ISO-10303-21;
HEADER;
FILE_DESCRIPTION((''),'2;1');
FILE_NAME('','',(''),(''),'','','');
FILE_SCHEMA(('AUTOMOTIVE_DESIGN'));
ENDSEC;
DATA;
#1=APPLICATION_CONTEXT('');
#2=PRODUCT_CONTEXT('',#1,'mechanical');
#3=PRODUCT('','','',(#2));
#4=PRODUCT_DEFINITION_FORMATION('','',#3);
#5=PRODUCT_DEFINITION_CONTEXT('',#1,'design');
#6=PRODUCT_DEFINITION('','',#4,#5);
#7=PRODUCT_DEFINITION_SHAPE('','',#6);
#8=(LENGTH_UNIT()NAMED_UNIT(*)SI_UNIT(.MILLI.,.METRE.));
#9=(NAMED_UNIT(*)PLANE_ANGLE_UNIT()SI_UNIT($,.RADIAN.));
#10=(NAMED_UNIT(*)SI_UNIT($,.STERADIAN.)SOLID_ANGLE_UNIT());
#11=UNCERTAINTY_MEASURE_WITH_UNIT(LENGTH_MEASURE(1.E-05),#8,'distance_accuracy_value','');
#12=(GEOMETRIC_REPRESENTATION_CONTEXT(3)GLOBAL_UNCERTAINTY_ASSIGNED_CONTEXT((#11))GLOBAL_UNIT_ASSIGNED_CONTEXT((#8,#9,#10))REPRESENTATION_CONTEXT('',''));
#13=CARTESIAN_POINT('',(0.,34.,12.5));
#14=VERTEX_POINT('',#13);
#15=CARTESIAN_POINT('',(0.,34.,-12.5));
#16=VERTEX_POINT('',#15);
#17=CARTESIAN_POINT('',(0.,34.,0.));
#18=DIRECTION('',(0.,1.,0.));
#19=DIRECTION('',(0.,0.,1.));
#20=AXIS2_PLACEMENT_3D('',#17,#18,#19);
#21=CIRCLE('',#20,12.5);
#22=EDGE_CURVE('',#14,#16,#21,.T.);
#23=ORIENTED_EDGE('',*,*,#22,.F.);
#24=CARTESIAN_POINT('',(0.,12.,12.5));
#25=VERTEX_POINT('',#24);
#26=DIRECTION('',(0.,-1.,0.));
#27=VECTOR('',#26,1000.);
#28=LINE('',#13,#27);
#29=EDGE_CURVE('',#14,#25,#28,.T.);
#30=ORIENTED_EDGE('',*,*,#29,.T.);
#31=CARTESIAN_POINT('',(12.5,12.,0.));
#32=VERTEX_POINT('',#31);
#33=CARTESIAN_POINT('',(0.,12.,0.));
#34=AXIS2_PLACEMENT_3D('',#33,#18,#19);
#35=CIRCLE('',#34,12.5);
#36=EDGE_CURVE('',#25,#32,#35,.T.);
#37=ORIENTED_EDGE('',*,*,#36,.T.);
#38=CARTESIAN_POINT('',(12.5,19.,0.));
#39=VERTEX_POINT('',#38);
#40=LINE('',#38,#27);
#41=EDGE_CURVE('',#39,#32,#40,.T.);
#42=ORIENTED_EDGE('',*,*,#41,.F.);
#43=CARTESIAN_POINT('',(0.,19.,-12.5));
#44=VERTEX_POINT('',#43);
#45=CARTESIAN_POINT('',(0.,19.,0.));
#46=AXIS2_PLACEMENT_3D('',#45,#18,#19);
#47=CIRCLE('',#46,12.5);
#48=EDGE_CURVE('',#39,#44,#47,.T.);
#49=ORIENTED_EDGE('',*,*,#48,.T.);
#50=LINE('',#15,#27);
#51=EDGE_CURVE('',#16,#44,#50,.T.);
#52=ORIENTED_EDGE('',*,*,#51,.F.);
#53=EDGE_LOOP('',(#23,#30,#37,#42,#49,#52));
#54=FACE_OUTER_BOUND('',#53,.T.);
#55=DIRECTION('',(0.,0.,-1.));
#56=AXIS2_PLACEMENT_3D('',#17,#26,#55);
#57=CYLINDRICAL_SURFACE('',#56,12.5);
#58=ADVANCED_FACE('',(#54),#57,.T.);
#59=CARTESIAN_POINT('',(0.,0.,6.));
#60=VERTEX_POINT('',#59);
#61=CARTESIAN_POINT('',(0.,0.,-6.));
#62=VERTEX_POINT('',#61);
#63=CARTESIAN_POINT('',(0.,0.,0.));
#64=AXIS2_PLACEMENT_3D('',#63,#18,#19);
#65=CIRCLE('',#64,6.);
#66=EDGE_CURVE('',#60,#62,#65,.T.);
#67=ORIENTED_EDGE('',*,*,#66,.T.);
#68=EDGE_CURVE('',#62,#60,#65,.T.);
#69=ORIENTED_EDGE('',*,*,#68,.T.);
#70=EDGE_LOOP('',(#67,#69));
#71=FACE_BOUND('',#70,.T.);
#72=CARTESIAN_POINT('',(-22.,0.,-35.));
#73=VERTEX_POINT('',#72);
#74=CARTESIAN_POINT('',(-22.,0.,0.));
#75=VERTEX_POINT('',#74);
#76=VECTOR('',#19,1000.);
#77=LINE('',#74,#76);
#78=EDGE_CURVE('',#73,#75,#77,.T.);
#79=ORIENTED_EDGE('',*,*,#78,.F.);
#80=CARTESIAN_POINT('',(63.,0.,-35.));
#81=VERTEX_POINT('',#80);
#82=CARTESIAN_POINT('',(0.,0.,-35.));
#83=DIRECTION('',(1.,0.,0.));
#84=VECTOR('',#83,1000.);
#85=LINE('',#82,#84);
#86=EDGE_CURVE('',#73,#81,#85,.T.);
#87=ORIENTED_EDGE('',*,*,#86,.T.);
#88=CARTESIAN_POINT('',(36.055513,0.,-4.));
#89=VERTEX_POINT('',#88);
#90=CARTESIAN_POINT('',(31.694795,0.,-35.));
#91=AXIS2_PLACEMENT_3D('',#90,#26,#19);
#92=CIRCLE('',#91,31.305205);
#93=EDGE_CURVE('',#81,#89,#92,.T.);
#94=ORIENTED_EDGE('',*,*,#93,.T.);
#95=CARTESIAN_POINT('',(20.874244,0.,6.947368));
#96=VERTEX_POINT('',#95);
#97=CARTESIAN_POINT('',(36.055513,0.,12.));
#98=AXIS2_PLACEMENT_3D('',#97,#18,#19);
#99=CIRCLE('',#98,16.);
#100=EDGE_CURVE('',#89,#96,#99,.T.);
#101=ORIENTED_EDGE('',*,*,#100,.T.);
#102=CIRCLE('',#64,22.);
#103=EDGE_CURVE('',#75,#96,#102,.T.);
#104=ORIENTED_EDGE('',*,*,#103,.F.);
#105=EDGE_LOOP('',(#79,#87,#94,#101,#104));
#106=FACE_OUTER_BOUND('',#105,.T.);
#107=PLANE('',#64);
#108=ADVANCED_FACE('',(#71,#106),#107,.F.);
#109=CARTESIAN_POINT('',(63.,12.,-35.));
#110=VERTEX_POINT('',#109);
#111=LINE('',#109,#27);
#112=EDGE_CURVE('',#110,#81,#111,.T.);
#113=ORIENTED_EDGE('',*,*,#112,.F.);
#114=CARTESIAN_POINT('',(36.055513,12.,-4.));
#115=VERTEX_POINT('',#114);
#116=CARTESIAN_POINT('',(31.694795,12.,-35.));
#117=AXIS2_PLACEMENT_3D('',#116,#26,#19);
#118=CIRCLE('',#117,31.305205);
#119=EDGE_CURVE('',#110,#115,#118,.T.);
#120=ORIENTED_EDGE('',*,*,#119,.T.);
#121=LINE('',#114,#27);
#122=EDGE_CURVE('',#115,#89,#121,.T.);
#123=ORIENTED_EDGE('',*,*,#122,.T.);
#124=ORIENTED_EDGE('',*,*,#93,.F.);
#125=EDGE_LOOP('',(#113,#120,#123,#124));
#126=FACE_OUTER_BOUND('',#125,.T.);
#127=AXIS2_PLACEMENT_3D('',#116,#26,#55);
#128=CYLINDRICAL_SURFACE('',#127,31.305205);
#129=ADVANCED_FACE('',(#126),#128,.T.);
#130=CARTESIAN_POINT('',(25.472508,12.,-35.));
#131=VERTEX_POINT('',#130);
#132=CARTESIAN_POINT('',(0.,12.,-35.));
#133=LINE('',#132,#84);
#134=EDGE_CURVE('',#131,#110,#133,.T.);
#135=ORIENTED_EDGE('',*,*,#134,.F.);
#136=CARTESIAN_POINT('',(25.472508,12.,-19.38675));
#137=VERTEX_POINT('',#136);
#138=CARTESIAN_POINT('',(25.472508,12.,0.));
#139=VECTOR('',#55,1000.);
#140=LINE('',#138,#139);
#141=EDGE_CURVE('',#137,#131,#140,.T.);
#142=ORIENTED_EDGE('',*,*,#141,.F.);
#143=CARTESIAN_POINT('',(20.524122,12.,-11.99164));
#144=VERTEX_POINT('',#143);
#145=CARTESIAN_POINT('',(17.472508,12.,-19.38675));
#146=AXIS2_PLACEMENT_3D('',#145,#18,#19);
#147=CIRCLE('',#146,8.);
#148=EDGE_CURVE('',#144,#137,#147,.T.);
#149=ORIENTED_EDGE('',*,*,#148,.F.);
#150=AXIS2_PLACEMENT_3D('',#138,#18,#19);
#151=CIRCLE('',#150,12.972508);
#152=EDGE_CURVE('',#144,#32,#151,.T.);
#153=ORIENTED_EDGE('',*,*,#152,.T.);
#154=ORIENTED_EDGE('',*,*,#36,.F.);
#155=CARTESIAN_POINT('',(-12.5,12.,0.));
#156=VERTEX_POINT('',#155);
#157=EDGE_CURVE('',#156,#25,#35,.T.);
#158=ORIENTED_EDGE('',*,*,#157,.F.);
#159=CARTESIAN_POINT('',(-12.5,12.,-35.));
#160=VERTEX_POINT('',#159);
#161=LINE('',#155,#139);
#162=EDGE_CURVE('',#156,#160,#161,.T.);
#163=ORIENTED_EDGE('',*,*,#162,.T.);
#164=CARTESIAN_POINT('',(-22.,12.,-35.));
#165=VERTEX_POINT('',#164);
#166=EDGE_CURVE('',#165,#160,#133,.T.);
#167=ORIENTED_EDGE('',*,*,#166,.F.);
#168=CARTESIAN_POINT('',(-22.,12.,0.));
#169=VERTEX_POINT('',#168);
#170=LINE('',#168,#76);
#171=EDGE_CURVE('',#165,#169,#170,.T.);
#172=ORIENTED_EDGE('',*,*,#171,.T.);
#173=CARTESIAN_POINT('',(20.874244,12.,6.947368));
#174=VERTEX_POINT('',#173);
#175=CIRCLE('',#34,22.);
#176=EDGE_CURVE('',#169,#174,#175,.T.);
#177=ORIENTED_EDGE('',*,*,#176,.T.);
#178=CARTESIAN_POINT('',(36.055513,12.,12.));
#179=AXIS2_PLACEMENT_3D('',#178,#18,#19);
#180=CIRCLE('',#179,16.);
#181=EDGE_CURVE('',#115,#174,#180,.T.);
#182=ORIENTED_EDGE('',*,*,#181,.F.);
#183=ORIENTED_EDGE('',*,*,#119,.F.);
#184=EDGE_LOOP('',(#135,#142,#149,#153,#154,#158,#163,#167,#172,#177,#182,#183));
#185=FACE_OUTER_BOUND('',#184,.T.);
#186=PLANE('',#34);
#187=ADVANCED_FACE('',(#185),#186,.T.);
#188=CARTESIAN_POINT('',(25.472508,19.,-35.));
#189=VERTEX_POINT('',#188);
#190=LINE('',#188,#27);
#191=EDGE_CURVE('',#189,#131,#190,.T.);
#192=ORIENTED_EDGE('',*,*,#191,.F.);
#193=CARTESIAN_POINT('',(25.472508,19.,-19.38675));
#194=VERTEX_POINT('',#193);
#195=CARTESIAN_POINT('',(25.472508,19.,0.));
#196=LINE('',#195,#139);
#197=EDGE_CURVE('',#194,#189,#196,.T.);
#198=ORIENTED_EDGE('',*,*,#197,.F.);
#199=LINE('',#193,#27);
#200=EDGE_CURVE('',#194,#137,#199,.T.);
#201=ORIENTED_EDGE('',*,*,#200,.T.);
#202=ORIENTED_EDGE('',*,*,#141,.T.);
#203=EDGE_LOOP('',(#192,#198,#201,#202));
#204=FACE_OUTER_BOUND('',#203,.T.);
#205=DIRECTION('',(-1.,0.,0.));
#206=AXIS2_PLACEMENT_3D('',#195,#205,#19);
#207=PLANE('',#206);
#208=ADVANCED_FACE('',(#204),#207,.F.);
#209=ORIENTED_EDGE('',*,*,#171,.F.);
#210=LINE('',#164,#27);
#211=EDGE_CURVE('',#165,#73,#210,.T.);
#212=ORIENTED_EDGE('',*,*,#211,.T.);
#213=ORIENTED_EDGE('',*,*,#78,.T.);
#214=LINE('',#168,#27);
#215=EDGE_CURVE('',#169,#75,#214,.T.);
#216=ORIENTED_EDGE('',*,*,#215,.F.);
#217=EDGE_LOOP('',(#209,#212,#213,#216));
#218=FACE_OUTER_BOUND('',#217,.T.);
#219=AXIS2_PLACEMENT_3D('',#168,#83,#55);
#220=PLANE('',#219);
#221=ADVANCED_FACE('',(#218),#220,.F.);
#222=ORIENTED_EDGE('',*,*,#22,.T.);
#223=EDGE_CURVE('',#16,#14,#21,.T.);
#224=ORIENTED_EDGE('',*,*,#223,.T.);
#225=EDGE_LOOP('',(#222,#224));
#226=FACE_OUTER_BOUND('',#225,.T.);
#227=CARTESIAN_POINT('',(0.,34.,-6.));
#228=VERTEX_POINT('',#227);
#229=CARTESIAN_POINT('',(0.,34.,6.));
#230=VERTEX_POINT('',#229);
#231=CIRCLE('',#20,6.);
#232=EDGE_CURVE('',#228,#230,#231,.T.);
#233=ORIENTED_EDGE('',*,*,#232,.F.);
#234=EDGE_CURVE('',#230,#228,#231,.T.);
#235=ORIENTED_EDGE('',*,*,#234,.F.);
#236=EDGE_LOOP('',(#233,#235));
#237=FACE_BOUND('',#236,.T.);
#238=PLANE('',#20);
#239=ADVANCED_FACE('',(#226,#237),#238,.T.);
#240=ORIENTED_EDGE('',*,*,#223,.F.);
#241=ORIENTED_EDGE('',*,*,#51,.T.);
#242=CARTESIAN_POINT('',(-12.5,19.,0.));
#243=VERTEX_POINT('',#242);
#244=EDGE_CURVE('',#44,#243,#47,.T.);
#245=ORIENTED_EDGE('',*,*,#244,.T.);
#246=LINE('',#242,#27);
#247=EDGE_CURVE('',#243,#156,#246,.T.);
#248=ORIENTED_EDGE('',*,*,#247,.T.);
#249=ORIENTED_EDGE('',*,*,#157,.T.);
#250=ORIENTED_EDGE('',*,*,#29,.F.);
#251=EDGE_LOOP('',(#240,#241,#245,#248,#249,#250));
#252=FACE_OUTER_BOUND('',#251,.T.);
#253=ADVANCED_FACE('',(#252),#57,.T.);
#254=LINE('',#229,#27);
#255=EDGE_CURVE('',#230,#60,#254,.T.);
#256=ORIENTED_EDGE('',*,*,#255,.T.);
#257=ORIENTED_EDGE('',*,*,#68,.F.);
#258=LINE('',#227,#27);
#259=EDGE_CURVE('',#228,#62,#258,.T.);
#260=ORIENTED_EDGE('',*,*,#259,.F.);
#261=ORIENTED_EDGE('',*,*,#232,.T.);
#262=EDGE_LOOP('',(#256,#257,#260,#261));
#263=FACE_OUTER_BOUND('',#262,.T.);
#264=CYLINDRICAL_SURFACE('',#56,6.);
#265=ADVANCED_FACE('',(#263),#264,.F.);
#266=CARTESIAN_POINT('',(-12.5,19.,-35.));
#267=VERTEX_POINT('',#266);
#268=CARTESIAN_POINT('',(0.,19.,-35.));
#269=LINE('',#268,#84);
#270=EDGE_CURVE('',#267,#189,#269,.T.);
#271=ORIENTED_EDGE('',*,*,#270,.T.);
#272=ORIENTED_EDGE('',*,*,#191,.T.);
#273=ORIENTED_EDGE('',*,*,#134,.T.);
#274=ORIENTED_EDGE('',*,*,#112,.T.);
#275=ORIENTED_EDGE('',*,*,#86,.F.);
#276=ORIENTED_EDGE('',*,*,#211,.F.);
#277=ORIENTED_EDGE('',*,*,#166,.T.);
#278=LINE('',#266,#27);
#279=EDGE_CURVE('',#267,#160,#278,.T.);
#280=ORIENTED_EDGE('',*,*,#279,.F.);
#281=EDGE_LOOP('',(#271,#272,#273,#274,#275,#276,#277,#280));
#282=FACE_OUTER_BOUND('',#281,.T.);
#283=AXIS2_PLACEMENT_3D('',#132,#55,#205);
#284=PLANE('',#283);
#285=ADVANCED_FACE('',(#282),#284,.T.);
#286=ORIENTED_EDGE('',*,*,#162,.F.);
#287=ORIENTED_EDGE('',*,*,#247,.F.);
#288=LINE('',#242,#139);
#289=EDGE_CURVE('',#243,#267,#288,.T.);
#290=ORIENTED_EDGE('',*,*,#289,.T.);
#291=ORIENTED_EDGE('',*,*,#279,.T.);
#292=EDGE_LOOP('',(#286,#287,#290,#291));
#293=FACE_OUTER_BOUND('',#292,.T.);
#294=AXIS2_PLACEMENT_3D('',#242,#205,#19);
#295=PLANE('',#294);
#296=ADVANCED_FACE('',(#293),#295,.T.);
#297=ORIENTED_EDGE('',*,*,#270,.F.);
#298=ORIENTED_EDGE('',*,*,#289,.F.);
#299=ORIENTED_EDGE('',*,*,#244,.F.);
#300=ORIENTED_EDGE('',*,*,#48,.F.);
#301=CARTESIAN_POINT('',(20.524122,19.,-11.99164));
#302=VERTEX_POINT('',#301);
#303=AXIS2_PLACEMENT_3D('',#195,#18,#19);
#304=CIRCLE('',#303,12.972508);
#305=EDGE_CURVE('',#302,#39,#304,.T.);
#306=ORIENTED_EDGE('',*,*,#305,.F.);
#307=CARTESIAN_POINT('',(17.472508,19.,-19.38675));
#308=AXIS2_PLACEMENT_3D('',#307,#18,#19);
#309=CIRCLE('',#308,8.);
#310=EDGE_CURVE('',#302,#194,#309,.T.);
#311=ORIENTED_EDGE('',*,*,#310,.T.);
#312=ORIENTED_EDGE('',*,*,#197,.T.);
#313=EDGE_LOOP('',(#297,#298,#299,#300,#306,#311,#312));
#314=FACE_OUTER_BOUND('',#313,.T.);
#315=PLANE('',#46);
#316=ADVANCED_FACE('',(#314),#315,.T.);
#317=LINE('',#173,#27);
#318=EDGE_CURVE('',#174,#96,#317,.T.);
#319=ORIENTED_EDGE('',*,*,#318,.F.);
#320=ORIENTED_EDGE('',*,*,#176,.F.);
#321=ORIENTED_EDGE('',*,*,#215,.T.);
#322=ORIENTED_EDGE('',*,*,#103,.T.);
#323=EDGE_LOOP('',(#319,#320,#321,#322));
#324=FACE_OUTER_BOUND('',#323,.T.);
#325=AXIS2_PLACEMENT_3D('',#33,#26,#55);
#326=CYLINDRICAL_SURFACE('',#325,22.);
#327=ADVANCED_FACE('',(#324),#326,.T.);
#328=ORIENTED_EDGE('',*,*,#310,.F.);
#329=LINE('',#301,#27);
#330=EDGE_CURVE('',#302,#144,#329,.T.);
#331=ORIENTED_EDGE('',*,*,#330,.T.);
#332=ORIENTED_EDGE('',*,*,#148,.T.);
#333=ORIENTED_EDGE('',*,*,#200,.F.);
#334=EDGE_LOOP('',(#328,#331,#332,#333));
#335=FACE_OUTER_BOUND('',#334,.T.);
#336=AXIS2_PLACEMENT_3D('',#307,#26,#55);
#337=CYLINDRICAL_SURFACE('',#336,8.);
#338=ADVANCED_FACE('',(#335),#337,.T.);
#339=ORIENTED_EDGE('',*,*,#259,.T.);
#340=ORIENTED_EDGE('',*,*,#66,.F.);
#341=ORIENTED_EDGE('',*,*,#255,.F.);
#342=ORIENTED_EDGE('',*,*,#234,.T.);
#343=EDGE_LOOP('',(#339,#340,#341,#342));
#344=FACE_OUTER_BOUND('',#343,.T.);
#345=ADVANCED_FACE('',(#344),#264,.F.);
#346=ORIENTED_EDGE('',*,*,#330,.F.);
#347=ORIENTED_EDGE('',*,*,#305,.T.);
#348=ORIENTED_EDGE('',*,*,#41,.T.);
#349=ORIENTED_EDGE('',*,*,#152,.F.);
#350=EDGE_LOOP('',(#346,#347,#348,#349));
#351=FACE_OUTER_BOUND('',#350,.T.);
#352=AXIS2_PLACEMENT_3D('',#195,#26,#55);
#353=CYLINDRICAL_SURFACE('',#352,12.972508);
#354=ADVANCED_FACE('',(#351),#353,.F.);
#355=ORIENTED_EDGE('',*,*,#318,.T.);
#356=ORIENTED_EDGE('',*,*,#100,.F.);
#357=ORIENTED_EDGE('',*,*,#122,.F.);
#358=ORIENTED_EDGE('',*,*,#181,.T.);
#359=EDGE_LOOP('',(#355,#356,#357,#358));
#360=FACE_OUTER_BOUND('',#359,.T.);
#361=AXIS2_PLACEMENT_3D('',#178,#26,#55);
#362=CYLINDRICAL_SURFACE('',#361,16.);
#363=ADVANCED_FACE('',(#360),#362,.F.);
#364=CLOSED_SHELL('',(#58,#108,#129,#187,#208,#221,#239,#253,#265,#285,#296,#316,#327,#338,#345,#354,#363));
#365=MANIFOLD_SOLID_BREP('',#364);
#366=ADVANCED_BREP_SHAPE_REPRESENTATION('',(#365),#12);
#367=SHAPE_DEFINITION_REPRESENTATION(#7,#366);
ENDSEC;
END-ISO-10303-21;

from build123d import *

# Parameters (mm, degrees)
BASE_PLATE_12MM_DEPTH = 12
RAISED_PAD_19MM_DEPTH = 19
HUB_PROFILE_R         = 12.5
HUB_PROFILE_R_2       = 6
HUB_BOSS_34MM_DEPTH   = 34


with BuildPart() as part:
    # Base Plate Profile → Base Plate 12mm (new body)
    with BuildSketch(Plane(origin=(0, 0, 0), x_dir=(1, 0, 0), z_dir=(0, 1, 0))):
        with BuildLine():
            Line((-12.5, 35), (-22, 35))
            Line((-22, 35), (-22, 0))
            ThreePointArc((-22, 0), (-3.518993252, -21.716737473), (20.874244226, -6.947368421))
            ThreePointArc((20.874244226, -6.947368421), (26.697150325, 0.97771369), (36.055512755, 4))
            ThreePointArc((36.055512755, 4), (55.322416794, 14.463414397), (63, 35))
            Line((63, 35), (25.47250751, 35))
            Line((25.47250751, 35), (25.47250751, 19.386749889))
            ThreePointArc((25.47250751, 19.386749889), (24.121301121, 14.937756348), (20.524121628, 11.991639932))
            ThreePointArc((20.524121628, 11.991639932), (14.69106688, 7.214325266), (12.5, 0))
            ThreePointArc((12.5, 0), (0, -12.5), (-12.5, 0))
            Line((-12.5, 0), (-12.5, 35))
        make_face()
    extrude(amount=BASE_PLATE_12MM_DEPTH)

    # Raised Pad Profile → Raised Pad 19mm (add)
    with BuildSketch(Plane(origin=(0, 0, 0), x_dir=(1, 0, 0), z_dir=(0, 1, 0))):
        with BuildLine():
            ThreePointArc((20.524121628, 11.991639932), (24.121301121, 14.937756348), (25.47250751, 19.386749889))
            Line((25.47250751, 19.386749889), (25.47250751, 35))
            Line((25.47250751, 35), (0, 35))
            Line((0, 35), (0, 12.5))
            ThreePointArc((0, 12.5), (8.838834765, 8.838834765), (12.5, 0))
            ThreePointArc((12.5, 0), (14.69106688, 7.214325266), (20.524121628, 11.991639932))
        make_face()
        with BuildLine():
            Line((0, 12.5), (0, 35))
            Line((0, 35), (-12.5, 35))
            Line((-12.5, 35), (-12.5, 0))
            ThreePointArc((-12.5, 0), (-8.838834765, 8.838834765), (0, 12.5))
        make_face()
    extrude(amount=RAISED_PAD_19MM_DEPTH)

    # Hub Profile → Hub Boss 34mm (add)
    with BuildSketch(Plane(origin=(0, 0, 0), x_dir=(1, 0, 0), z_dir=(0, 1, 0))):
        Circle(HUB_PROFILE_R)
        with Locations(Location((0, 0, 0), (0, 0, 270))):
            Circle(HUB_PROFILE_R_2, mode=Mode.SUBTRACT)
    extrude(amount=HUB_BOSS_34MM_DEPTH)


solid = part.part
